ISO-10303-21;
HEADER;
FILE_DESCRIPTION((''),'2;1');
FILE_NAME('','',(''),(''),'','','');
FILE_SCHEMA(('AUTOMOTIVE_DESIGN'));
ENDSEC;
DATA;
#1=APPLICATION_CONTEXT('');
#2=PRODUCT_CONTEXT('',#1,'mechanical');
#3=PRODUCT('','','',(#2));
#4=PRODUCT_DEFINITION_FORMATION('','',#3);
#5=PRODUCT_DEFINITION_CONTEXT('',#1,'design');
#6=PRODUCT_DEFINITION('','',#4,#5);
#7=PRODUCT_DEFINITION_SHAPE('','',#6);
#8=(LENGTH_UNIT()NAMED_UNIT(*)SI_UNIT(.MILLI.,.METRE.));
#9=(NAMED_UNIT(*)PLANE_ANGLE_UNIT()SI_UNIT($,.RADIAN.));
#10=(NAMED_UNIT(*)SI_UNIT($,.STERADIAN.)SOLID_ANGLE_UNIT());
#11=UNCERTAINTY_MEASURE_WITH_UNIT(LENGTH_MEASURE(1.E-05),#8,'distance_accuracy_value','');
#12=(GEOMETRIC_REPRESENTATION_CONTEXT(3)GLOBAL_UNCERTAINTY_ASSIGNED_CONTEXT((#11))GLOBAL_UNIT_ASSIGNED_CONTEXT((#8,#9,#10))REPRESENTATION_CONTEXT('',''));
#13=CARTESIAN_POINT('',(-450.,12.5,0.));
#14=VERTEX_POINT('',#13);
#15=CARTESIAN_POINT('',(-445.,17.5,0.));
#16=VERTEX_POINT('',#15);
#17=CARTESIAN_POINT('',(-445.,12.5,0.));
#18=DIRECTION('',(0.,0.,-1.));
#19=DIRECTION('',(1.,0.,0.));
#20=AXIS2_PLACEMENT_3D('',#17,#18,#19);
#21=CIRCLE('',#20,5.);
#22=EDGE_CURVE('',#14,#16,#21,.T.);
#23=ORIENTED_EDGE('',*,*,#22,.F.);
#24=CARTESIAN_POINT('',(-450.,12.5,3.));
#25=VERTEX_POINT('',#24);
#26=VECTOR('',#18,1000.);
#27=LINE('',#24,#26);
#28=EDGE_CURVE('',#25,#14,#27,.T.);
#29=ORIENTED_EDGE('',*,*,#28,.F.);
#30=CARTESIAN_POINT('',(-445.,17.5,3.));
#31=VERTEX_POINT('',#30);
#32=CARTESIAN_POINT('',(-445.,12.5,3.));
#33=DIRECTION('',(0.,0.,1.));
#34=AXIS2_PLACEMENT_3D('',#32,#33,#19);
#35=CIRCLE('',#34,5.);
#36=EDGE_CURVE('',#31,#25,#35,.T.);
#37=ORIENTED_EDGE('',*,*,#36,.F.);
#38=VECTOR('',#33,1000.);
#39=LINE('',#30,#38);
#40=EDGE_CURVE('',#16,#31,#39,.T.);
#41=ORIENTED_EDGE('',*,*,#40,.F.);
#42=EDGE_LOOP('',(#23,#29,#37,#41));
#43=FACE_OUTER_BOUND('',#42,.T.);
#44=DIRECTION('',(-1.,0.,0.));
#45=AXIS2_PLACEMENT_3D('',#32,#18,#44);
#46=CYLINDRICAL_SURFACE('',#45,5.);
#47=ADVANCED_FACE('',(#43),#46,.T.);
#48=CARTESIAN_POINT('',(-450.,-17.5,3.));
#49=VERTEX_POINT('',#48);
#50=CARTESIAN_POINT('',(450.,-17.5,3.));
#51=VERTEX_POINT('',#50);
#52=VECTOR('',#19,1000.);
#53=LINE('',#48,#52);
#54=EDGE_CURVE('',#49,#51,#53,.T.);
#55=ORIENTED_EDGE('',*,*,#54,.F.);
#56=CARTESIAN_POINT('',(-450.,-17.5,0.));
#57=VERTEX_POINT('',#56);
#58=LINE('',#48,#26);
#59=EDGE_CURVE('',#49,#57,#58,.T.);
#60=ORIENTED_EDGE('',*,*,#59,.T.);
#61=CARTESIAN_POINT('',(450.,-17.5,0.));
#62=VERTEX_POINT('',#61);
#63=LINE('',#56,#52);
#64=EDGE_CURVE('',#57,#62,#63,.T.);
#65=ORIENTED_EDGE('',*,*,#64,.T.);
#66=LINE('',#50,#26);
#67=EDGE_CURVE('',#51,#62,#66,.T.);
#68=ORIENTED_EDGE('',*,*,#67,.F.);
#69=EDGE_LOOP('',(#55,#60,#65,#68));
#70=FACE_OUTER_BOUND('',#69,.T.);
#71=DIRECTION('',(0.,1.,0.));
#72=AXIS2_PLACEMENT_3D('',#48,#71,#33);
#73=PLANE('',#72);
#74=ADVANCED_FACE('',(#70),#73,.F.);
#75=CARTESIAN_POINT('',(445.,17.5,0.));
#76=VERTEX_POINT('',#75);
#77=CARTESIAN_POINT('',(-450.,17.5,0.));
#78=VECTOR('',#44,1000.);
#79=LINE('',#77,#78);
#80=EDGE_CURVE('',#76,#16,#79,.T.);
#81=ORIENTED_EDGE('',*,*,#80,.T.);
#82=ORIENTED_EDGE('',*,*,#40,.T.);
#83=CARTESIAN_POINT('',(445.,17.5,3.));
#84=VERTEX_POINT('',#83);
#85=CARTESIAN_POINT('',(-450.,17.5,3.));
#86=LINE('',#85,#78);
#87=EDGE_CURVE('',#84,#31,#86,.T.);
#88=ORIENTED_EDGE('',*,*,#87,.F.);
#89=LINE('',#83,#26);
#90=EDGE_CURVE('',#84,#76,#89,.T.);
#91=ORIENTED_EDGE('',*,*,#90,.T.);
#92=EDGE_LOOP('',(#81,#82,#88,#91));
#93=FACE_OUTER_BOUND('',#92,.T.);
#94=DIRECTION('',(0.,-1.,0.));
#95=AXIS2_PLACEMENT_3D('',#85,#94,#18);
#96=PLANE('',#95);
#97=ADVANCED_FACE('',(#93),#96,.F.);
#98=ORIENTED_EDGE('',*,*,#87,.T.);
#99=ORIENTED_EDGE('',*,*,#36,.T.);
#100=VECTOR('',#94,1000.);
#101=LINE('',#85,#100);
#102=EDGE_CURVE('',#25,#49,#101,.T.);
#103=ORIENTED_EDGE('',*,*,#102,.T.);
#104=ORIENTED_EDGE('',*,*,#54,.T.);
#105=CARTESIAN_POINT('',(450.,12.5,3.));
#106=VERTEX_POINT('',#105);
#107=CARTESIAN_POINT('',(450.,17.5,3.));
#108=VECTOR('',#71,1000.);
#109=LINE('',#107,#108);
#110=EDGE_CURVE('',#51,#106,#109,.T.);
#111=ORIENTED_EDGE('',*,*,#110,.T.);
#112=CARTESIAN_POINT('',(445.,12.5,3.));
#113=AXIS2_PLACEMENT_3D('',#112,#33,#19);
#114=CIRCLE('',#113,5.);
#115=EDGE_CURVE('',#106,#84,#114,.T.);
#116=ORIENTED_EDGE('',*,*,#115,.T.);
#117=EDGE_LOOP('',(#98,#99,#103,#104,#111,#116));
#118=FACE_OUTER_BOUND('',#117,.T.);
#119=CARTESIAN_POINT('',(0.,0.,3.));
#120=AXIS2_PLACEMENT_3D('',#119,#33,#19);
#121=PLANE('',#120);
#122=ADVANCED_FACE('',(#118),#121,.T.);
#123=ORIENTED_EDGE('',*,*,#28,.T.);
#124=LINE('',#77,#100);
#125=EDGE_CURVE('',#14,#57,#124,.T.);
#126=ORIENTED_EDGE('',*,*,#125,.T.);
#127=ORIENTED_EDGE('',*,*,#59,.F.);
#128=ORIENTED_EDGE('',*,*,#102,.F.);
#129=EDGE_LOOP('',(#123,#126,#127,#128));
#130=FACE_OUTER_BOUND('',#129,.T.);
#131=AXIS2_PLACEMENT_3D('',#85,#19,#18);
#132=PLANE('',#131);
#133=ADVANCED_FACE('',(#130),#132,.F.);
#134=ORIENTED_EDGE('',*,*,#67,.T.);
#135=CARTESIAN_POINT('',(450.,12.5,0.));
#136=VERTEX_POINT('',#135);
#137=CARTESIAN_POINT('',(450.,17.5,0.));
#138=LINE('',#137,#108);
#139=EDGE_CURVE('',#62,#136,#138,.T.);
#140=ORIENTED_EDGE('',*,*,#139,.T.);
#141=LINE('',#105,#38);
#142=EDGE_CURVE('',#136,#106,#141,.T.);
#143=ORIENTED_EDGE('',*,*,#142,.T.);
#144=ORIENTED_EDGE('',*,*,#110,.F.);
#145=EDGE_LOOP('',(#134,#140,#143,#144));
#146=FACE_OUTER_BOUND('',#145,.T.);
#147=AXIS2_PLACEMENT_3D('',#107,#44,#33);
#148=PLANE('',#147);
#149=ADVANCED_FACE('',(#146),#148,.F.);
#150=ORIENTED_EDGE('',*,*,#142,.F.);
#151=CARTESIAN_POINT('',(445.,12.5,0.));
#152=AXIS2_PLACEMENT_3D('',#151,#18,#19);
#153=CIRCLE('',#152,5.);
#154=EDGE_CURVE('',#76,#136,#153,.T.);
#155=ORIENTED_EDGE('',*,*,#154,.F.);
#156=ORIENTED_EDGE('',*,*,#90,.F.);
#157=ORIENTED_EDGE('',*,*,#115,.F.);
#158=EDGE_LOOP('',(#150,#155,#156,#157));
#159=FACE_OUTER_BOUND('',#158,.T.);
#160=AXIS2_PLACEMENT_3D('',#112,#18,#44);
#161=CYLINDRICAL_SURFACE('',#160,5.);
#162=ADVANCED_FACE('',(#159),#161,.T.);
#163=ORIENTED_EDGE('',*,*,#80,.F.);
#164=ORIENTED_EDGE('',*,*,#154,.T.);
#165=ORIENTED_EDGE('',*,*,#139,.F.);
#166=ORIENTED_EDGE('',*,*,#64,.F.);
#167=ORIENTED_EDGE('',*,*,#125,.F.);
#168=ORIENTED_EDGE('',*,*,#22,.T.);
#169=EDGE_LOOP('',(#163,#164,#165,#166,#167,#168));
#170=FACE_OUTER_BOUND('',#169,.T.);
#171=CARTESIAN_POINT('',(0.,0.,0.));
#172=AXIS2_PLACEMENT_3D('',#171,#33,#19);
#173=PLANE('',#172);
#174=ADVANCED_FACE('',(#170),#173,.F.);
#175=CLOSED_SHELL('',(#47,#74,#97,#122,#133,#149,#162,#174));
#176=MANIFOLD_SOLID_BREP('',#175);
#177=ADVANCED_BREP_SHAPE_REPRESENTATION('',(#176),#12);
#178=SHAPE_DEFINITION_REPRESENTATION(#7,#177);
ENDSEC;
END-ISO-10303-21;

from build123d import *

# Parameters (mm, degrees)
SKETCH_1_W      = 900
SKETCH_1_H      = 35
EXTRUDE_1_DEPTH = 3
FILLET_1_R      = 5


with BuildPart() as part:
    # 草图1 → 凸台-拉伸1 (new body)
    with BuildSketch(Plane.XY):
        Rectangle(SKETCH_1_W, SKETCH_1_H)
    extrude(amount=EXTRUDE_1_DEPTH)

    # 圆角1
    fillet_1_edges = [part.edges().sort_by_distance(p)[0] for p in [
        (-450, 17.5, 1.5),
        (450, 17.5, 1.5),
    ]]
    fillet(fillet_1_edges, radius=FILLET_1_R)


solid = part.part
